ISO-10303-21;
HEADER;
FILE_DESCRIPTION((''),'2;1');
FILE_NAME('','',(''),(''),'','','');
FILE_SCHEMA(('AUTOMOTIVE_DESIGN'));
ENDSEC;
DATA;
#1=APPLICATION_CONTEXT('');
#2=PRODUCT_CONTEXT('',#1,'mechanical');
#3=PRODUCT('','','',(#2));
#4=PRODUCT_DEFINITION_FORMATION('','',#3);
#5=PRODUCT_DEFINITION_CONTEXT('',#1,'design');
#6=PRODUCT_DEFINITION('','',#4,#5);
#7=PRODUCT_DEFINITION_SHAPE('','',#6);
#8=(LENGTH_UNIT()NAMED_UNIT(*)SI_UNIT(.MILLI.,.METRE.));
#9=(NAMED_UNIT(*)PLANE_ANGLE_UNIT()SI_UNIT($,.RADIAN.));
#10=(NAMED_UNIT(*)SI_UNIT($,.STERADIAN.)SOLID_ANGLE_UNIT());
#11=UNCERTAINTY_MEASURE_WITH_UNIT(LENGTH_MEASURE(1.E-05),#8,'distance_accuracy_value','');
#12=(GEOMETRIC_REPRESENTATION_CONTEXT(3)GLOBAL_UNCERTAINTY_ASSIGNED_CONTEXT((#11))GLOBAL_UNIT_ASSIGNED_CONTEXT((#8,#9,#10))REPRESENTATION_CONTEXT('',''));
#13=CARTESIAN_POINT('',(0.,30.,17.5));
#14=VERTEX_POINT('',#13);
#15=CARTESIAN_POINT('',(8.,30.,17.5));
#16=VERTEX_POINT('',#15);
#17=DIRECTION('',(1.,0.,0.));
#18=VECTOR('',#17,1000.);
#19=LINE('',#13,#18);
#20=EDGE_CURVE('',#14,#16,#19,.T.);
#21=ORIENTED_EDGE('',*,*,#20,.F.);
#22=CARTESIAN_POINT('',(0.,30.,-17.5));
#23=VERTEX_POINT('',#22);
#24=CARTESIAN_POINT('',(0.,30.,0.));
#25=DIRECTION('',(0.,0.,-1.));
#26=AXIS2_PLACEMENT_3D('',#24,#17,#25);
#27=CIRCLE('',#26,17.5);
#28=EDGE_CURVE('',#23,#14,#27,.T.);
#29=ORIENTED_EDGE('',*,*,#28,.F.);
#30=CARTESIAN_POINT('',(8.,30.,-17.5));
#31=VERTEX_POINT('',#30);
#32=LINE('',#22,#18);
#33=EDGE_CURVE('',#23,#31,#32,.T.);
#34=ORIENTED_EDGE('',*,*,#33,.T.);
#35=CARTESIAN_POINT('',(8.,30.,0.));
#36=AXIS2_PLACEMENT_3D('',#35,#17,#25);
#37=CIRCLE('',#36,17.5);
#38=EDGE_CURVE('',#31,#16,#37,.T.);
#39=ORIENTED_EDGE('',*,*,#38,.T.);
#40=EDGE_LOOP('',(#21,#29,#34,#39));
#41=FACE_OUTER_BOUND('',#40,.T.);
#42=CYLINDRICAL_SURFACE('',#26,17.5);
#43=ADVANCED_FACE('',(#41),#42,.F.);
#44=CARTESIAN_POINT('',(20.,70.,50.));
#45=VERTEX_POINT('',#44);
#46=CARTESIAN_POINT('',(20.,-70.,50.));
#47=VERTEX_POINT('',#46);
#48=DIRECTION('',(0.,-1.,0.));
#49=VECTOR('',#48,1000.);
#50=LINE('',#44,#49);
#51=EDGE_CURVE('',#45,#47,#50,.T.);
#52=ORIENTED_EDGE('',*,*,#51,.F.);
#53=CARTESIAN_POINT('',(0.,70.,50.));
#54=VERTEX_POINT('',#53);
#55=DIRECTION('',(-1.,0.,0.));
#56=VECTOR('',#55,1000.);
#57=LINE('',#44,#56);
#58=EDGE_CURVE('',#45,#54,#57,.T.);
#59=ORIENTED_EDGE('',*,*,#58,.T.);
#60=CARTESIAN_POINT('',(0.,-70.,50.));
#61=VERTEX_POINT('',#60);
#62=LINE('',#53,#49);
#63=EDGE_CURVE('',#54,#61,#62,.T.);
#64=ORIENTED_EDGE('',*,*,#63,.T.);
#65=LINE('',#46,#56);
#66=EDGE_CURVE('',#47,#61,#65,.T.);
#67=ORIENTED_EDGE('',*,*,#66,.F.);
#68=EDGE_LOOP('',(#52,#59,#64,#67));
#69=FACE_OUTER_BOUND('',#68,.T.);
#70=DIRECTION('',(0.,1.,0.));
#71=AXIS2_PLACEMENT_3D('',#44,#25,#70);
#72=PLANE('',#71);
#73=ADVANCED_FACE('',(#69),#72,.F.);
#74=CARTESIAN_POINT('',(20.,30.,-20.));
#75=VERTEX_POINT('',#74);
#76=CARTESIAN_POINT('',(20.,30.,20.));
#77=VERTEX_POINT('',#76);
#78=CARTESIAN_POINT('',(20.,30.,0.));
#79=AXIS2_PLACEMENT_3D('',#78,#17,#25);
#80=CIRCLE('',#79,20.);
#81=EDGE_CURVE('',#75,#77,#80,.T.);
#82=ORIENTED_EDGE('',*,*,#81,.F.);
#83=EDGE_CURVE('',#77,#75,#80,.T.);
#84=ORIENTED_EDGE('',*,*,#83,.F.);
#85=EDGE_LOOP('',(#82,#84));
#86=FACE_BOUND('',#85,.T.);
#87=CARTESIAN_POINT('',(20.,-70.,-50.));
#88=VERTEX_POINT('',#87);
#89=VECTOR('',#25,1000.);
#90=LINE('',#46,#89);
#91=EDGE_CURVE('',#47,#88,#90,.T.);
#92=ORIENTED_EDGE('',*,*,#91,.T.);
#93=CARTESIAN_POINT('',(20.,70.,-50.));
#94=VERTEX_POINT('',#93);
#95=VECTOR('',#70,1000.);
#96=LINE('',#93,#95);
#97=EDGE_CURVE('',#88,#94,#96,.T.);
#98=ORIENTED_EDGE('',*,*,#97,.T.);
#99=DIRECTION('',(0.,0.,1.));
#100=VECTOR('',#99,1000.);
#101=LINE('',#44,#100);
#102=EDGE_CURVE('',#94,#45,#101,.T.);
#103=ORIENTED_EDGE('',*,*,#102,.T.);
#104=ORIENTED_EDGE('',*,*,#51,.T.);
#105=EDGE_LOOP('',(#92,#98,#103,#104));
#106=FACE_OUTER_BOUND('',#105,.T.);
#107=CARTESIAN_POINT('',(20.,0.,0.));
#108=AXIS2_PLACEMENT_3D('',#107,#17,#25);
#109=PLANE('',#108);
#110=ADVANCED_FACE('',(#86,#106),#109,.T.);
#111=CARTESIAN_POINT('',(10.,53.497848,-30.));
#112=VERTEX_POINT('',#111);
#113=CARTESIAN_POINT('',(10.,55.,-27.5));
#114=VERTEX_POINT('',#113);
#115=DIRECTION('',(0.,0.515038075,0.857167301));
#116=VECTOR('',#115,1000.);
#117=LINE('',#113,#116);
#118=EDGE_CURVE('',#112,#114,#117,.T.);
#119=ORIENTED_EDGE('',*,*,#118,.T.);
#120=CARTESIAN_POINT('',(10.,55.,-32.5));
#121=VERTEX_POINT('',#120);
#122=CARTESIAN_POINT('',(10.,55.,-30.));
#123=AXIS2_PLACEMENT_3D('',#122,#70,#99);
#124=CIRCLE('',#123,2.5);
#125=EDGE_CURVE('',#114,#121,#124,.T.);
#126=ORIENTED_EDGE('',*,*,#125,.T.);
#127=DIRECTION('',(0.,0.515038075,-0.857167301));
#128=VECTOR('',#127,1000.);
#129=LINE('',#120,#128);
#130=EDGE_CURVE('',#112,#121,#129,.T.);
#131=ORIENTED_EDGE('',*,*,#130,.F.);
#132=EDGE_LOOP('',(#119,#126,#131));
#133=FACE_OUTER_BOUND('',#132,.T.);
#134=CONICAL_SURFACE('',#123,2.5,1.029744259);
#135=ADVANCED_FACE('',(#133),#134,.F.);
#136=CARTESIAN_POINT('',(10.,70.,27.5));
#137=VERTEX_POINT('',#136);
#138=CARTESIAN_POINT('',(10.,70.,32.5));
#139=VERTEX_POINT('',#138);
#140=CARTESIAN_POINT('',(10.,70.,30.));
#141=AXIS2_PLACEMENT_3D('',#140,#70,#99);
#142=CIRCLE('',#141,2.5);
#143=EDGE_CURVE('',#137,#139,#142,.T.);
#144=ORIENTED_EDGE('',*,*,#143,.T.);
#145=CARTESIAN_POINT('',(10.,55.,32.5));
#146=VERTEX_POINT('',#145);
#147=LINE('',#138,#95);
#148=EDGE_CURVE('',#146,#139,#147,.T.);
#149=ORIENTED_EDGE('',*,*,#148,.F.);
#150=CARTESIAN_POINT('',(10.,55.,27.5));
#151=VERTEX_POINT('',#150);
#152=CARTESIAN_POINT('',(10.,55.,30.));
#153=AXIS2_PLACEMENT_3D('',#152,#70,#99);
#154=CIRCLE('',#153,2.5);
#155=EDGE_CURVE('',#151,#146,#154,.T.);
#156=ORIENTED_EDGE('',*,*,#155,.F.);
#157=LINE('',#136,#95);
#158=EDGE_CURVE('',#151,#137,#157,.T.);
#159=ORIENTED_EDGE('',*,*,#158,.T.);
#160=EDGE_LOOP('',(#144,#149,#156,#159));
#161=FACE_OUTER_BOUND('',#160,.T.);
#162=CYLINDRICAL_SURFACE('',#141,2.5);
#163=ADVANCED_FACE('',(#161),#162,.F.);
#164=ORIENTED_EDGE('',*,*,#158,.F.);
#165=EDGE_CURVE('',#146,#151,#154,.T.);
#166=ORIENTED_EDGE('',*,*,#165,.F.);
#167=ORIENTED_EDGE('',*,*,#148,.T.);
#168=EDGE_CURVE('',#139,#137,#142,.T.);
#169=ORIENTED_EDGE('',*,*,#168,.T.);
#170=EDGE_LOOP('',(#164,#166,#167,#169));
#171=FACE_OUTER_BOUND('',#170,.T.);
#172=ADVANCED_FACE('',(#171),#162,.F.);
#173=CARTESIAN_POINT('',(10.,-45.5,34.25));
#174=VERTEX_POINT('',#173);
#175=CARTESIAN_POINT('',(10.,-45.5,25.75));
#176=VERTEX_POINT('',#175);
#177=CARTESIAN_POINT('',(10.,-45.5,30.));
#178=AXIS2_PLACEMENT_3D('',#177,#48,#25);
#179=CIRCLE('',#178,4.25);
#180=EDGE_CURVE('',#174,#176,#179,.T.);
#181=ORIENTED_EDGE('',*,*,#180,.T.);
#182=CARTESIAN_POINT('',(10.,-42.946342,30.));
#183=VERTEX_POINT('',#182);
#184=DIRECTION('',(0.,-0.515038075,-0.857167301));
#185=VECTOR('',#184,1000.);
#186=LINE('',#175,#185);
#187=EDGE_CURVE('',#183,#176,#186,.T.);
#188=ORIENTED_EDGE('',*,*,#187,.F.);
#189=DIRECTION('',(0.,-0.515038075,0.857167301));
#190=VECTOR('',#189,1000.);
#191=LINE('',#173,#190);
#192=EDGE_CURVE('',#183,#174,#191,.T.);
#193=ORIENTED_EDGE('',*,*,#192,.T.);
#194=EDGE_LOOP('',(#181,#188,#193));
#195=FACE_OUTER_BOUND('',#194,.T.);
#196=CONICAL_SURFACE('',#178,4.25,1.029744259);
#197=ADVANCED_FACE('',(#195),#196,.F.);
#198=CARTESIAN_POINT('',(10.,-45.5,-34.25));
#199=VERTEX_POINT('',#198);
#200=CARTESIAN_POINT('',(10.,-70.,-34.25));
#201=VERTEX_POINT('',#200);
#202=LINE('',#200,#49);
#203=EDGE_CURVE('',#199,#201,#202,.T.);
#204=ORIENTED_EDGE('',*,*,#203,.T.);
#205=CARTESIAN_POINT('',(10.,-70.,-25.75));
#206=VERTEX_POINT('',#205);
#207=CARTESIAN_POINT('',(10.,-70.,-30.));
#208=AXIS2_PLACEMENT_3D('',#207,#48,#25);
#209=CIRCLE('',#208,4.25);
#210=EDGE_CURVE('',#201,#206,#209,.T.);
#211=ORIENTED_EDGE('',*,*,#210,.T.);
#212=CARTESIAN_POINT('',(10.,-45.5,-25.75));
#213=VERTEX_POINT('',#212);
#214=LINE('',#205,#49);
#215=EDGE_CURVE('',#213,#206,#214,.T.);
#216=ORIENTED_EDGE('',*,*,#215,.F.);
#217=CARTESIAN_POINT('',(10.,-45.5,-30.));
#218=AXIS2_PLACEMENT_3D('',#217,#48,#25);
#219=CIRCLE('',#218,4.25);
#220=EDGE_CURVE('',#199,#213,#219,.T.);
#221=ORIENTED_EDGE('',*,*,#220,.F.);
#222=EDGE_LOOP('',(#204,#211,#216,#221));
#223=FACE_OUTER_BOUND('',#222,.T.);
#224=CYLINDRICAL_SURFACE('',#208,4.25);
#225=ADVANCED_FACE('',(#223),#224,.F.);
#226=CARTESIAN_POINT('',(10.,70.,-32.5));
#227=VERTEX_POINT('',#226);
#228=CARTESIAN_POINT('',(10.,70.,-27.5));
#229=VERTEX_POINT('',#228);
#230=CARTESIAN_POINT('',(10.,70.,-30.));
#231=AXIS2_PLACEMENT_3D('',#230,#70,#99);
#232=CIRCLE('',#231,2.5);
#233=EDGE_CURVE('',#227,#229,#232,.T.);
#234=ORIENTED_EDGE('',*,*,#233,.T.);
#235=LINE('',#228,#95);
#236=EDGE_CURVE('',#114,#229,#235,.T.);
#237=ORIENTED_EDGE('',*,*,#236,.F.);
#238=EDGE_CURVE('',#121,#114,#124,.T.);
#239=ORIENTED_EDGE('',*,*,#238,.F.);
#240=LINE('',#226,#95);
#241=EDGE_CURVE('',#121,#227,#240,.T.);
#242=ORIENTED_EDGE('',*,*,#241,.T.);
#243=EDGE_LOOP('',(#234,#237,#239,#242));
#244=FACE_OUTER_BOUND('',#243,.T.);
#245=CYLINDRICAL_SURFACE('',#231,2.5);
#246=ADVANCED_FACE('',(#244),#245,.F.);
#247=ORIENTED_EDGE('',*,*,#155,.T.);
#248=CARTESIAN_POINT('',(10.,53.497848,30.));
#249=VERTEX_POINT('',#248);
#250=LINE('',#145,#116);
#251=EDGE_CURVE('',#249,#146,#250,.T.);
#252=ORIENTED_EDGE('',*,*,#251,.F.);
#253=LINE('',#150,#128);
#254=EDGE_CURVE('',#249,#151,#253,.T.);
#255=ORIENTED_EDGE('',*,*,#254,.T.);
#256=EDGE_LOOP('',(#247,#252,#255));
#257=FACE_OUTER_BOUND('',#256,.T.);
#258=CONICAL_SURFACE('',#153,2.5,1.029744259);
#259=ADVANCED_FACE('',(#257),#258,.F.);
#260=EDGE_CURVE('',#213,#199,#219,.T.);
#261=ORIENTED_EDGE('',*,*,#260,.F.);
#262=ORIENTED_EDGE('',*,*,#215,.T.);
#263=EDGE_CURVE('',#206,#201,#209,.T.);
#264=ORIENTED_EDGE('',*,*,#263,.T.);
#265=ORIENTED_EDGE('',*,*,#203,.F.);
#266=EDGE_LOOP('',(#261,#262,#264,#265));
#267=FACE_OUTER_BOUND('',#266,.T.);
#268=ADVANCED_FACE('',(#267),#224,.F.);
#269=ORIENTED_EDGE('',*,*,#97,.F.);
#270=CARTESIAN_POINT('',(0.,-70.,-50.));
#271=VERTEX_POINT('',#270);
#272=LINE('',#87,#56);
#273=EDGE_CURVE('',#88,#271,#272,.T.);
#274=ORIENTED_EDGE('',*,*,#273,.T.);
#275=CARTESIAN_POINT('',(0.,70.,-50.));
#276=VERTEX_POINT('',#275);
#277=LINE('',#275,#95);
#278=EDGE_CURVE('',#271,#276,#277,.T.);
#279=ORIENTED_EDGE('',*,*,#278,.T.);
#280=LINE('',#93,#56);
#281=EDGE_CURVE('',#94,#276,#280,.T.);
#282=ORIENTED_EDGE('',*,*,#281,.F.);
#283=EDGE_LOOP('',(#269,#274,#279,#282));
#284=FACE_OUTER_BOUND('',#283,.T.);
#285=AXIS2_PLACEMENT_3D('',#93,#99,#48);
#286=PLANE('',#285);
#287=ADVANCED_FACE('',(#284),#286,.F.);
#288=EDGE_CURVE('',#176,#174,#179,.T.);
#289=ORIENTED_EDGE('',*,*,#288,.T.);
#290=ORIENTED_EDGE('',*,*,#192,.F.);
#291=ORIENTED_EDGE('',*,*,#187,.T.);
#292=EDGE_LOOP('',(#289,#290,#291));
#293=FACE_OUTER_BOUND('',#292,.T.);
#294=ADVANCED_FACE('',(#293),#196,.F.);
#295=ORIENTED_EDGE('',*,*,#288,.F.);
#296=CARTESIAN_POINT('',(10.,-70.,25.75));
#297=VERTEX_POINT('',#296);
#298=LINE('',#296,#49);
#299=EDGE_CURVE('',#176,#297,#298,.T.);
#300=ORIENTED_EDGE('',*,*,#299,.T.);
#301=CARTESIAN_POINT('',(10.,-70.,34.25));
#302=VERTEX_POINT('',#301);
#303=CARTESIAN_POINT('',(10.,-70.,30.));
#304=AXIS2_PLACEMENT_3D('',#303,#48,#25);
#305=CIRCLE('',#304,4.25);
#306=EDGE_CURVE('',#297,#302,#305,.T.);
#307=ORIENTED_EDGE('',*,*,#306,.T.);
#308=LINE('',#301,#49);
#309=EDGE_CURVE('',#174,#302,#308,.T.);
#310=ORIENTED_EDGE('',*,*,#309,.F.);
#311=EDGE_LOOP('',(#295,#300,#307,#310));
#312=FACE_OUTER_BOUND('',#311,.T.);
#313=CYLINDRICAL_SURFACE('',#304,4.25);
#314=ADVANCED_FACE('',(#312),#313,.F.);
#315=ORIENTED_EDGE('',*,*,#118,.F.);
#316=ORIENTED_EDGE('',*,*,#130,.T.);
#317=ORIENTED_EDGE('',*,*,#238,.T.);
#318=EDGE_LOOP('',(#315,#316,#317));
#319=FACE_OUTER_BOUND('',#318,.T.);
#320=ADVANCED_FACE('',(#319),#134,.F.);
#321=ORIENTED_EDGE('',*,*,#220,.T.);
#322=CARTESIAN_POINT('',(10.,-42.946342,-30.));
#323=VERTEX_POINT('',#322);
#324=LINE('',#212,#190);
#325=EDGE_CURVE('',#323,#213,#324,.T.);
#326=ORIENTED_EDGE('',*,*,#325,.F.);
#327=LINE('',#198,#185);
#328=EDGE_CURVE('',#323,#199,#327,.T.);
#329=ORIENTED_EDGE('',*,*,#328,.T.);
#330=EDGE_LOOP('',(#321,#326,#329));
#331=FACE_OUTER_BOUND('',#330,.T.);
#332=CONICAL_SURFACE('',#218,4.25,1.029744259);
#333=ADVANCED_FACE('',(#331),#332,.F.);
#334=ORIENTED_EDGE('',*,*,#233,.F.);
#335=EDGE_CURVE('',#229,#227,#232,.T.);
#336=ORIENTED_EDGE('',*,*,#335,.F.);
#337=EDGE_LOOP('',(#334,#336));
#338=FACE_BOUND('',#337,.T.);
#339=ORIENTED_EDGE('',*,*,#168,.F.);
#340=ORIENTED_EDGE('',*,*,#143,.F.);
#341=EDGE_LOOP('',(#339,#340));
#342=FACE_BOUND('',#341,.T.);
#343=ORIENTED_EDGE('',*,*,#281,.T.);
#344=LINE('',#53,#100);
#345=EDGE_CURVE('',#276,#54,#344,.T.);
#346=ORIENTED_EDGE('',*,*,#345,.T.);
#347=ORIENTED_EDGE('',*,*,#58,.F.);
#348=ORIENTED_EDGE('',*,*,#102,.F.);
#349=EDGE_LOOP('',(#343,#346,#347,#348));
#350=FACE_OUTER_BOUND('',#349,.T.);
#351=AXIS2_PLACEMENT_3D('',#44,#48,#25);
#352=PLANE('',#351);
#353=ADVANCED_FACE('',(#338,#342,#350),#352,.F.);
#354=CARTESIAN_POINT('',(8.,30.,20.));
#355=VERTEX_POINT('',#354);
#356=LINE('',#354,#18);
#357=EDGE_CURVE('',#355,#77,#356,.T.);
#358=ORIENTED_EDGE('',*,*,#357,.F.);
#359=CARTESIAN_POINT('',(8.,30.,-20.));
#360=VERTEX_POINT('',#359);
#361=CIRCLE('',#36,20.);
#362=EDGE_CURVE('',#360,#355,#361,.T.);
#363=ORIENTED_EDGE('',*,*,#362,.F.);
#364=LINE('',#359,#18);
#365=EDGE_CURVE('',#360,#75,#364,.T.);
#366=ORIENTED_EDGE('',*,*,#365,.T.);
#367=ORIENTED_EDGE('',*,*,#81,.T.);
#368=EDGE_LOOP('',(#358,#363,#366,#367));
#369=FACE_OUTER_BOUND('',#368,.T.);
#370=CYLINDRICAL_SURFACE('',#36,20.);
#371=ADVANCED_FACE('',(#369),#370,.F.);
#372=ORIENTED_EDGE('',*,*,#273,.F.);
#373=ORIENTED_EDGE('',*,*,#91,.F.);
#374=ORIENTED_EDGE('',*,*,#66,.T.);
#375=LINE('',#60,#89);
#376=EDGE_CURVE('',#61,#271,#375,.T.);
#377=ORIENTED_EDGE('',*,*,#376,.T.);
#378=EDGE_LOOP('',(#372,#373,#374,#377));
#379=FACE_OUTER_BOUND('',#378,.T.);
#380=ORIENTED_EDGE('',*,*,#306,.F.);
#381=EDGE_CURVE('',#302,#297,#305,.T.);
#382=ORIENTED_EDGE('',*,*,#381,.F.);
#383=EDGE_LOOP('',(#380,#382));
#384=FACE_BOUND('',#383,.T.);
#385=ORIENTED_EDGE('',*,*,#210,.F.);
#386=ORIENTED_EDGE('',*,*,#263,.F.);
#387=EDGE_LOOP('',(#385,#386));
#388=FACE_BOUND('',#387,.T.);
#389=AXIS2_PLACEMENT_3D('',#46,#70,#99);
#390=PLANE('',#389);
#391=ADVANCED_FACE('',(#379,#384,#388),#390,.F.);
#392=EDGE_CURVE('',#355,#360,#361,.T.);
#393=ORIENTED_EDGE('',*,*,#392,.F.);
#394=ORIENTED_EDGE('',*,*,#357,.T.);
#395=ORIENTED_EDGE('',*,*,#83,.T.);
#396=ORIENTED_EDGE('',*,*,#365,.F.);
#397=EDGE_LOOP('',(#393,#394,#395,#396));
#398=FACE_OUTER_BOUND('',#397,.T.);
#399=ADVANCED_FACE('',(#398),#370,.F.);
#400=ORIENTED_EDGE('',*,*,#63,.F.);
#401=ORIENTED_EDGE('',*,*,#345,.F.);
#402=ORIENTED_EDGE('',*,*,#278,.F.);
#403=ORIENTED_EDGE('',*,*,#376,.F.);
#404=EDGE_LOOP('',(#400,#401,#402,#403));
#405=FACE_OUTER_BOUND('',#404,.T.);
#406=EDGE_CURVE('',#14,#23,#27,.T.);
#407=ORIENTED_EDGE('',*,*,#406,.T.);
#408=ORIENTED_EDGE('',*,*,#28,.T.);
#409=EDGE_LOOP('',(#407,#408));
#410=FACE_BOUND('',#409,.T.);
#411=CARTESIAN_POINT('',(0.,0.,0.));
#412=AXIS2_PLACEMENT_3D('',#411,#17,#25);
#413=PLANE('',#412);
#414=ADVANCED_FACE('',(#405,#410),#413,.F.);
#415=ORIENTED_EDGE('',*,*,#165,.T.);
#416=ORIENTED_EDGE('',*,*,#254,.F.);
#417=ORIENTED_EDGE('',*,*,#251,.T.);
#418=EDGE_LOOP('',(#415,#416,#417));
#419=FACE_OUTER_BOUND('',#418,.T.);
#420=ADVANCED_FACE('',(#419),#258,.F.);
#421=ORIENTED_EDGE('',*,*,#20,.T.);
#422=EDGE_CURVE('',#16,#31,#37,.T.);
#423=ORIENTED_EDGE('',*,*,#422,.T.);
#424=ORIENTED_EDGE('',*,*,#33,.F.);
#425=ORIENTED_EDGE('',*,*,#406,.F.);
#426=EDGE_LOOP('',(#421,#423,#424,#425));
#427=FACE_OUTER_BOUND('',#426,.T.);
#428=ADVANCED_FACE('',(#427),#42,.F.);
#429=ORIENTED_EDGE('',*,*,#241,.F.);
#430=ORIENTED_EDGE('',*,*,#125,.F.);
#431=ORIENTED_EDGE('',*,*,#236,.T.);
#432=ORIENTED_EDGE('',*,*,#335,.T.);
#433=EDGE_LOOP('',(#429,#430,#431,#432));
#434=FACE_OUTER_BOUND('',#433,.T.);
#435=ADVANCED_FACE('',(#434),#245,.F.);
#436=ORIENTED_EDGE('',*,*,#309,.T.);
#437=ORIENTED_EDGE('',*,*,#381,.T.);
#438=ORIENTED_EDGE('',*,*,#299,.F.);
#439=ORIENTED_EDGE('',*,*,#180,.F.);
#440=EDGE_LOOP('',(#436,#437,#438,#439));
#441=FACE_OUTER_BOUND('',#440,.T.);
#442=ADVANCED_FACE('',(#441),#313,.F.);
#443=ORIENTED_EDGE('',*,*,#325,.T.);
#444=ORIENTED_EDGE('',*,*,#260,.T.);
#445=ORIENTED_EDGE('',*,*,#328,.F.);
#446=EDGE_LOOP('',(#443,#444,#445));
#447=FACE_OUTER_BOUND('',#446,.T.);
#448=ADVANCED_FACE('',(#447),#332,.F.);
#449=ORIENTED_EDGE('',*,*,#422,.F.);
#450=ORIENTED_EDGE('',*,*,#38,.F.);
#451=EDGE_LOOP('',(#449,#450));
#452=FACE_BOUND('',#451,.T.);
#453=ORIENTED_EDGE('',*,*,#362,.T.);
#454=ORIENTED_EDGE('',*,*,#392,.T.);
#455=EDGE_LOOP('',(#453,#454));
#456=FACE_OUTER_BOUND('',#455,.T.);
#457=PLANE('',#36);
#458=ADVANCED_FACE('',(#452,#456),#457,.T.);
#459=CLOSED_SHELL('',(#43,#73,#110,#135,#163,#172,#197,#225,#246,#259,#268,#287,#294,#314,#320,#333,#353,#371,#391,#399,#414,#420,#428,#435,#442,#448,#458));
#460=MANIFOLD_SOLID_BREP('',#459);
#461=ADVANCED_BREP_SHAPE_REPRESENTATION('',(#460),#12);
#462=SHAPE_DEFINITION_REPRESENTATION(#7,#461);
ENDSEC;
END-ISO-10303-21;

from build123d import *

# Parameters (mm, degrees)
SKETCH_1_W              = 100
SKETCH_1_H              = 140
EXTRUDE_1_DEPTH         = 20
HOLE_WIZARD_M10_1_D     = 8.5
HOLE_WIZARD_M10_1_DEPTH = 24.5
HOLE_WIZARD_M10_1_TIP   = 2.553657631
SKETCH_4_R              = 20
CUT_EXTRUDE_1_DEPTH     = 12
SKETCH_5_R              = 17.5
CUT_EXTRUDE_2_DEPTH     = 87.856203002
HOLE_WIZARD_M6_1_D      = 5
HOLE_WIZARD_M6_1_DEPTH  = 15
HOLE_WIZARD_M6_1_TIP    = 1.502151548


with BuildPart() as part:
    # 草图1 → 凸台-拉伸1 (new body)
    with BuildSketch(Plane(origin=(0, 0, 0), x_dir=(0, 0, -1), z_dir=(1, 0, 0))):
        Rectangle(SKETCH_1_W, SKETCH_1_H)
    extrude(amount=EXTRUDE_1_DEPTH)

    # M10 螺纹孔1
    with Locations(Plane(origin=(0, -70, 0), x_dir=(-1, 0, 0), z_dir=(0, -1, 0))):
        with Locations((-10, 30), (-10, -30)):
            Hole(HOLE_WIZARD_M10_1_D / 2, depth=HOLE_WIZARD_M10_1_DEPTH)
            with Locations((0, 0, -(HOLE_WIZARD_M10_1_DEPTH + HOLE_WIZARD_M10_1_TIP / 2))):  # 118° drill point
                Cone(0, HOLE_WIZARD_M10_1_D / 2, HOLE_WIZARD_M10_1_TIP, mode=Mode.SUBTRACT)

    # 草图4 → 切除-拉伸1 (cut)
    with BuildSketch(Plane(origin=(20, 0, 0), x_dir=(0, 0, -1), z_dir=(1, 0, 0))):
        with Locations((0, 30)):
            Circle(SKETCH_4_R)
    extrude(amount=-CUT_EXTRUDE_1_DEPTH, mode=Mode.SUBTRACT)

    # 草图5 → 切除-拉伸2 (cut, through all)
    with BuildSketch(Plane(origin=(8, 0, 0), x_dir=(0, 0, -1), z_dir=(1, 0, 0))):
        with Locations((0, 30)):
            Circle(SKETCH_5_R)
    extrude(amount=-CUT_EXTRUDE_2_DEPTH, mode=Mode.SUBTRACT)

    # M6 螺纹孔1
    with Locations(Plane(origin=(0, 70, 0), x_dir=(1, 0, 0), z_dir=(0, 1, 0))):
        with Locations((10, 30), (10, -30)):
            Hole(HOLE_WIZARD_M6_1_D / 2, depth=HOLE_WIZARD_M6_1_DEPTH)
            with Locations((0, 0, -(HOLE_WIZARD_M6_1_DEPTH + HOLE_WIZARD_M6_1_TIP / 2))):  # 118° drill point
                Cone(0, HOLE_WIZARD_M6_1_D / 2, HOLE_WIZARD_M6_1_TIP, mode=Mode.SUBTRACT)


solid = part.part
